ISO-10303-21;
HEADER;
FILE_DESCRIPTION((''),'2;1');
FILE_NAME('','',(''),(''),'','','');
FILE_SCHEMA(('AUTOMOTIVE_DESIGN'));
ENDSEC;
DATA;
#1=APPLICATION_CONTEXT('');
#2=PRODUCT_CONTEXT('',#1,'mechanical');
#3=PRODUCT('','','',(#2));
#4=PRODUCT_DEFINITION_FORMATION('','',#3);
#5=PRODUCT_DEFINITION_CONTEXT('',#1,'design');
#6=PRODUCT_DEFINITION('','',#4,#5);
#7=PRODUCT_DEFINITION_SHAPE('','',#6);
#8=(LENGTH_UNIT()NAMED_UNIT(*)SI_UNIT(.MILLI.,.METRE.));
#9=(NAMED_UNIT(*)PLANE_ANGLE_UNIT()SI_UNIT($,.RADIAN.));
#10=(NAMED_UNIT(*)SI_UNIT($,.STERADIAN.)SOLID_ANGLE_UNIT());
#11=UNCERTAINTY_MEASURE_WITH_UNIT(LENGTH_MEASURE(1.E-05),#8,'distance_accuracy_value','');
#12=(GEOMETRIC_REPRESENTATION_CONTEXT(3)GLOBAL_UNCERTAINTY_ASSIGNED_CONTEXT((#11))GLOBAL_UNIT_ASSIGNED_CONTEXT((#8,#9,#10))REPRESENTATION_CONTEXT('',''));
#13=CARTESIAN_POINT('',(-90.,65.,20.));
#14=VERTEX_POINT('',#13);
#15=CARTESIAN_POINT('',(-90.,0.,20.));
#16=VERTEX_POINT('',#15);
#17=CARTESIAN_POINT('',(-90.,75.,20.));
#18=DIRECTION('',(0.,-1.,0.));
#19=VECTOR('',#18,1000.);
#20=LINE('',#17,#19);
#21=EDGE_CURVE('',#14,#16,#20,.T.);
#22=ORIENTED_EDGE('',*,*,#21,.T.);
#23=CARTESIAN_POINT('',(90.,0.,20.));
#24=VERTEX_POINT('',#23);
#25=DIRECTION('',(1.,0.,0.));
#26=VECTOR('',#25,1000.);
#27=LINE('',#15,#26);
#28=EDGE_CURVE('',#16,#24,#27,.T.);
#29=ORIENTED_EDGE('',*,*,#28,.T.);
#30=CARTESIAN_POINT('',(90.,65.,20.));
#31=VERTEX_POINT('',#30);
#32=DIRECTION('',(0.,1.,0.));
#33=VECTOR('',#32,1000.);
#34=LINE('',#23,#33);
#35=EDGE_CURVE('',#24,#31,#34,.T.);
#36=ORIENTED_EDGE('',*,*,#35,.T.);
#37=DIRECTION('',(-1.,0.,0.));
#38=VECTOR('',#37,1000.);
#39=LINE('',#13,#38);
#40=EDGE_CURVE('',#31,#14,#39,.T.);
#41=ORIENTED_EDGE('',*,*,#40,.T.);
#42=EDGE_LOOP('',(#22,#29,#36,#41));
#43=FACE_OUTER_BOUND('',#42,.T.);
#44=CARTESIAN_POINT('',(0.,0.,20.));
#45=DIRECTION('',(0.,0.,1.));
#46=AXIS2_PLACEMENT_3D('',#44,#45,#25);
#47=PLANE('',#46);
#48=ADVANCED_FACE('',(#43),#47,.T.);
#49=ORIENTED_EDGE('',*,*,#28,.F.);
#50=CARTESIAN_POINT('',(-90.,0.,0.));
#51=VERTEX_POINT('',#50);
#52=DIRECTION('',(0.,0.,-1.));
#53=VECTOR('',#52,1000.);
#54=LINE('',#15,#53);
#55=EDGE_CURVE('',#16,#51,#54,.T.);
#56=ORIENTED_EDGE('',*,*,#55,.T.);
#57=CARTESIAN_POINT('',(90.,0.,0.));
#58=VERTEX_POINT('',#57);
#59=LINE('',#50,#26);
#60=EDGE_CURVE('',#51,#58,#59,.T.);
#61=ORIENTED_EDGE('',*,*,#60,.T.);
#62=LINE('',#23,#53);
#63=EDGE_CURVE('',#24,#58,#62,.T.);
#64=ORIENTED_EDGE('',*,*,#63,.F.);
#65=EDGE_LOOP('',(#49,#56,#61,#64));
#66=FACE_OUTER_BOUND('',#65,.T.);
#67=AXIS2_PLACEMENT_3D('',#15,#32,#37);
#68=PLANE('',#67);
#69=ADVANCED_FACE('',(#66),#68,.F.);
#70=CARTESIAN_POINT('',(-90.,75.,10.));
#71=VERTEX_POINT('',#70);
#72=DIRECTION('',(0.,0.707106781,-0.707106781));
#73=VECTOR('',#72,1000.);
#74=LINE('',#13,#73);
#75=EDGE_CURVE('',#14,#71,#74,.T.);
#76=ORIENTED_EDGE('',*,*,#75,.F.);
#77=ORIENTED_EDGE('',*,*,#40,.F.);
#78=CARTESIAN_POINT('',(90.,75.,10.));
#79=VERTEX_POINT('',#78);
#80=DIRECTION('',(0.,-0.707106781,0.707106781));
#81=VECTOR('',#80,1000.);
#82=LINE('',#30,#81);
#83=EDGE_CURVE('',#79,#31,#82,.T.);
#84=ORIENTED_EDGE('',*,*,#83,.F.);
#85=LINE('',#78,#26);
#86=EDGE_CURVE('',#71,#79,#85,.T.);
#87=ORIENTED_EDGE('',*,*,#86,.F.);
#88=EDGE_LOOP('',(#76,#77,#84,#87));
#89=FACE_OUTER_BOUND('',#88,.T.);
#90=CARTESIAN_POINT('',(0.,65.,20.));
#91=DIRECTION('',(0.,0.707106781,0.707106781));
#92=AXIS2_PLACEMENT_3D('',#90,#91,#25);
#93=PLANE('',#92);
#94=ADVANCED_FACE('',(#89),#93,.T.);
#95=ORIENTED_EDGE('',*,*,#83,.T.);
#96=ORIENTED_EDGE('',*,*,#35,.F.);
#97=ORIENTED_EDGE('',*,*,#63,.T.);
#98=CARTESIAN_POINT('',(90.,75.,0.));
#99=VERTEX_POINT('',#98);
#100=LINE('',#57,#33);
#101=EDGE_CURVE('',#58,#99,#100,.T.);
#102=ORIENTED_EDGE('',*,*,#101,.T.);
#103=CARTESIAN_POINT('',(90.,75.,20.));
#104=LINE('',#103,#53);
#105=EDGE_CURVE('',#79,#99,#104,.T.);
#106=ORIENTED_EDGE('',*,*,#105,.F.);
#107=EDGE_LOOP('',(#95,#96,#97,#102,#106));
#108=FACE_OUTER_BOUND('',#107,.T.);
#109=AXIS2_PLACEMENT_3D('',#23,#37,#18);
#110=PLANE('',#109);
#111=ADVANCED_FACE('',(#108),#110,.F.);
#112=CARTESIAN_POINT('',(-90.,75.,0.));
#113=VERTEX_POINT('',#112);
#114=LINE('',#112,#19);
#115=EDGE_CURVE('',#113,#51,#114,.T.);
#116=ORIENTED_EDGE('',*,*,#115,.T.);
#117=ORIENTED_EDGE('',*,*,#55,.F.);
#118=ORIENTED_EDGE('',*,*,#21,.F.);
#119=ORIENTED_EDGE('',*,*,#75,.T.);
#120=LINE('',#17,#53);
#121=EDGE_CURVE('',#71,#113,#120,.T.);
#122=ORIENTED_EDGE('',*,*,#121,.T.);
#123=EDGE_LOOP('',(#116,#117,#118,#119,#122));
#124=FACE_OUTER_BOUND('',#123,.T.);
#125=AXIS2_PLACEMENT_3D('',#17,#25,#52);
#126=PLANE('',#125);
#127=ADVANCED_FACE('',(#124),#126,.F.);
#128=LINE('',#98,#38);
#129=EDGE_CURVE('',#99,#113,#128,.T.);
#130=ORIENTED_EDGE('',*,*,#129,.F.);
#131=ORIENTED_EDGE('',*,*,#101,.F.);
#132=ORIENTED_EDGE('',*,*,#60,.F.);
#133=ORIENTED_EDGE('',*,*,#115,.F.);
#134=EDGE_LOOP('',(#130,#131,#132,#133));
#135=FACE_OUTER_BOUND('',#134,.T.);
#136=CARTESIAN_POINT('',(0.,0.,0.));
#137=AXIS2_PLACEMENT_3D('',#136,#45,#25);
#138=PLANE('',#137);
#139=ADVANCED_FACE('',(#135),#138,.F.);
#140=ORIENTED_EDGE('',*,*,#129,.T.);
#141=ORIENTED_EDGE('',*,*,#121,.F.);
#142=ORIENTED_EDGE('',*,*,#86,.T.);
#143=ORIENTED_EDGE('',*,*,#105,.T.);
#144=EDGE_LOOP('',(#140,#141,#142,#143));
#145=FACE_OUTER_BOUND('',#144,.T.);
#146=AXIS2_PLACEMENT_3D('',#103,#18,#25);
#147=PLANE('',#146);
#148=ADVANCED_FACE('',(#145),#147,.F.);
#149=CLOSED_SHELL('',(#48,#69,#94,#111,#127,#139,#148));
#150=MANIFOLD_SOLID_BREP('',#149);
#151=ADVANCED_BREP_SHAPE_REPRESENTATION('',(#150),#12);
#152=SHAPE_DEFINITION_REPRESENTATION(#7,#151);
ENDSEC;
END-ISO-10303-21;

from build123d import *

# Parameters (mm, degrees)
SKETCH_1_W      = 180
SKETCH_1_H      = 75
EXTRUDE_1_DEPTH = 20
CHAMFER_2_SIZE  = 10


with BuildPart() as part:
    # 草图1 → 凸台-拉伸1 (new body)
    with BuildSketch(Plane.XY):
        with Locations((0, 37.5)):
            Rectangle(SKETCH_1_W, SKETCH_1_H)
    extrude(amount=EXTRUDE_1_DEPTH)

    # 倒角2
    chamfer_2_edges = [part.edges().sort_by_distance(p)[0] for p in [
        (0, 75, 20),
    ]]
    chamfer(chamfer_2_edges, length=CHAMFER_2_SIZE)


solid = part.part
